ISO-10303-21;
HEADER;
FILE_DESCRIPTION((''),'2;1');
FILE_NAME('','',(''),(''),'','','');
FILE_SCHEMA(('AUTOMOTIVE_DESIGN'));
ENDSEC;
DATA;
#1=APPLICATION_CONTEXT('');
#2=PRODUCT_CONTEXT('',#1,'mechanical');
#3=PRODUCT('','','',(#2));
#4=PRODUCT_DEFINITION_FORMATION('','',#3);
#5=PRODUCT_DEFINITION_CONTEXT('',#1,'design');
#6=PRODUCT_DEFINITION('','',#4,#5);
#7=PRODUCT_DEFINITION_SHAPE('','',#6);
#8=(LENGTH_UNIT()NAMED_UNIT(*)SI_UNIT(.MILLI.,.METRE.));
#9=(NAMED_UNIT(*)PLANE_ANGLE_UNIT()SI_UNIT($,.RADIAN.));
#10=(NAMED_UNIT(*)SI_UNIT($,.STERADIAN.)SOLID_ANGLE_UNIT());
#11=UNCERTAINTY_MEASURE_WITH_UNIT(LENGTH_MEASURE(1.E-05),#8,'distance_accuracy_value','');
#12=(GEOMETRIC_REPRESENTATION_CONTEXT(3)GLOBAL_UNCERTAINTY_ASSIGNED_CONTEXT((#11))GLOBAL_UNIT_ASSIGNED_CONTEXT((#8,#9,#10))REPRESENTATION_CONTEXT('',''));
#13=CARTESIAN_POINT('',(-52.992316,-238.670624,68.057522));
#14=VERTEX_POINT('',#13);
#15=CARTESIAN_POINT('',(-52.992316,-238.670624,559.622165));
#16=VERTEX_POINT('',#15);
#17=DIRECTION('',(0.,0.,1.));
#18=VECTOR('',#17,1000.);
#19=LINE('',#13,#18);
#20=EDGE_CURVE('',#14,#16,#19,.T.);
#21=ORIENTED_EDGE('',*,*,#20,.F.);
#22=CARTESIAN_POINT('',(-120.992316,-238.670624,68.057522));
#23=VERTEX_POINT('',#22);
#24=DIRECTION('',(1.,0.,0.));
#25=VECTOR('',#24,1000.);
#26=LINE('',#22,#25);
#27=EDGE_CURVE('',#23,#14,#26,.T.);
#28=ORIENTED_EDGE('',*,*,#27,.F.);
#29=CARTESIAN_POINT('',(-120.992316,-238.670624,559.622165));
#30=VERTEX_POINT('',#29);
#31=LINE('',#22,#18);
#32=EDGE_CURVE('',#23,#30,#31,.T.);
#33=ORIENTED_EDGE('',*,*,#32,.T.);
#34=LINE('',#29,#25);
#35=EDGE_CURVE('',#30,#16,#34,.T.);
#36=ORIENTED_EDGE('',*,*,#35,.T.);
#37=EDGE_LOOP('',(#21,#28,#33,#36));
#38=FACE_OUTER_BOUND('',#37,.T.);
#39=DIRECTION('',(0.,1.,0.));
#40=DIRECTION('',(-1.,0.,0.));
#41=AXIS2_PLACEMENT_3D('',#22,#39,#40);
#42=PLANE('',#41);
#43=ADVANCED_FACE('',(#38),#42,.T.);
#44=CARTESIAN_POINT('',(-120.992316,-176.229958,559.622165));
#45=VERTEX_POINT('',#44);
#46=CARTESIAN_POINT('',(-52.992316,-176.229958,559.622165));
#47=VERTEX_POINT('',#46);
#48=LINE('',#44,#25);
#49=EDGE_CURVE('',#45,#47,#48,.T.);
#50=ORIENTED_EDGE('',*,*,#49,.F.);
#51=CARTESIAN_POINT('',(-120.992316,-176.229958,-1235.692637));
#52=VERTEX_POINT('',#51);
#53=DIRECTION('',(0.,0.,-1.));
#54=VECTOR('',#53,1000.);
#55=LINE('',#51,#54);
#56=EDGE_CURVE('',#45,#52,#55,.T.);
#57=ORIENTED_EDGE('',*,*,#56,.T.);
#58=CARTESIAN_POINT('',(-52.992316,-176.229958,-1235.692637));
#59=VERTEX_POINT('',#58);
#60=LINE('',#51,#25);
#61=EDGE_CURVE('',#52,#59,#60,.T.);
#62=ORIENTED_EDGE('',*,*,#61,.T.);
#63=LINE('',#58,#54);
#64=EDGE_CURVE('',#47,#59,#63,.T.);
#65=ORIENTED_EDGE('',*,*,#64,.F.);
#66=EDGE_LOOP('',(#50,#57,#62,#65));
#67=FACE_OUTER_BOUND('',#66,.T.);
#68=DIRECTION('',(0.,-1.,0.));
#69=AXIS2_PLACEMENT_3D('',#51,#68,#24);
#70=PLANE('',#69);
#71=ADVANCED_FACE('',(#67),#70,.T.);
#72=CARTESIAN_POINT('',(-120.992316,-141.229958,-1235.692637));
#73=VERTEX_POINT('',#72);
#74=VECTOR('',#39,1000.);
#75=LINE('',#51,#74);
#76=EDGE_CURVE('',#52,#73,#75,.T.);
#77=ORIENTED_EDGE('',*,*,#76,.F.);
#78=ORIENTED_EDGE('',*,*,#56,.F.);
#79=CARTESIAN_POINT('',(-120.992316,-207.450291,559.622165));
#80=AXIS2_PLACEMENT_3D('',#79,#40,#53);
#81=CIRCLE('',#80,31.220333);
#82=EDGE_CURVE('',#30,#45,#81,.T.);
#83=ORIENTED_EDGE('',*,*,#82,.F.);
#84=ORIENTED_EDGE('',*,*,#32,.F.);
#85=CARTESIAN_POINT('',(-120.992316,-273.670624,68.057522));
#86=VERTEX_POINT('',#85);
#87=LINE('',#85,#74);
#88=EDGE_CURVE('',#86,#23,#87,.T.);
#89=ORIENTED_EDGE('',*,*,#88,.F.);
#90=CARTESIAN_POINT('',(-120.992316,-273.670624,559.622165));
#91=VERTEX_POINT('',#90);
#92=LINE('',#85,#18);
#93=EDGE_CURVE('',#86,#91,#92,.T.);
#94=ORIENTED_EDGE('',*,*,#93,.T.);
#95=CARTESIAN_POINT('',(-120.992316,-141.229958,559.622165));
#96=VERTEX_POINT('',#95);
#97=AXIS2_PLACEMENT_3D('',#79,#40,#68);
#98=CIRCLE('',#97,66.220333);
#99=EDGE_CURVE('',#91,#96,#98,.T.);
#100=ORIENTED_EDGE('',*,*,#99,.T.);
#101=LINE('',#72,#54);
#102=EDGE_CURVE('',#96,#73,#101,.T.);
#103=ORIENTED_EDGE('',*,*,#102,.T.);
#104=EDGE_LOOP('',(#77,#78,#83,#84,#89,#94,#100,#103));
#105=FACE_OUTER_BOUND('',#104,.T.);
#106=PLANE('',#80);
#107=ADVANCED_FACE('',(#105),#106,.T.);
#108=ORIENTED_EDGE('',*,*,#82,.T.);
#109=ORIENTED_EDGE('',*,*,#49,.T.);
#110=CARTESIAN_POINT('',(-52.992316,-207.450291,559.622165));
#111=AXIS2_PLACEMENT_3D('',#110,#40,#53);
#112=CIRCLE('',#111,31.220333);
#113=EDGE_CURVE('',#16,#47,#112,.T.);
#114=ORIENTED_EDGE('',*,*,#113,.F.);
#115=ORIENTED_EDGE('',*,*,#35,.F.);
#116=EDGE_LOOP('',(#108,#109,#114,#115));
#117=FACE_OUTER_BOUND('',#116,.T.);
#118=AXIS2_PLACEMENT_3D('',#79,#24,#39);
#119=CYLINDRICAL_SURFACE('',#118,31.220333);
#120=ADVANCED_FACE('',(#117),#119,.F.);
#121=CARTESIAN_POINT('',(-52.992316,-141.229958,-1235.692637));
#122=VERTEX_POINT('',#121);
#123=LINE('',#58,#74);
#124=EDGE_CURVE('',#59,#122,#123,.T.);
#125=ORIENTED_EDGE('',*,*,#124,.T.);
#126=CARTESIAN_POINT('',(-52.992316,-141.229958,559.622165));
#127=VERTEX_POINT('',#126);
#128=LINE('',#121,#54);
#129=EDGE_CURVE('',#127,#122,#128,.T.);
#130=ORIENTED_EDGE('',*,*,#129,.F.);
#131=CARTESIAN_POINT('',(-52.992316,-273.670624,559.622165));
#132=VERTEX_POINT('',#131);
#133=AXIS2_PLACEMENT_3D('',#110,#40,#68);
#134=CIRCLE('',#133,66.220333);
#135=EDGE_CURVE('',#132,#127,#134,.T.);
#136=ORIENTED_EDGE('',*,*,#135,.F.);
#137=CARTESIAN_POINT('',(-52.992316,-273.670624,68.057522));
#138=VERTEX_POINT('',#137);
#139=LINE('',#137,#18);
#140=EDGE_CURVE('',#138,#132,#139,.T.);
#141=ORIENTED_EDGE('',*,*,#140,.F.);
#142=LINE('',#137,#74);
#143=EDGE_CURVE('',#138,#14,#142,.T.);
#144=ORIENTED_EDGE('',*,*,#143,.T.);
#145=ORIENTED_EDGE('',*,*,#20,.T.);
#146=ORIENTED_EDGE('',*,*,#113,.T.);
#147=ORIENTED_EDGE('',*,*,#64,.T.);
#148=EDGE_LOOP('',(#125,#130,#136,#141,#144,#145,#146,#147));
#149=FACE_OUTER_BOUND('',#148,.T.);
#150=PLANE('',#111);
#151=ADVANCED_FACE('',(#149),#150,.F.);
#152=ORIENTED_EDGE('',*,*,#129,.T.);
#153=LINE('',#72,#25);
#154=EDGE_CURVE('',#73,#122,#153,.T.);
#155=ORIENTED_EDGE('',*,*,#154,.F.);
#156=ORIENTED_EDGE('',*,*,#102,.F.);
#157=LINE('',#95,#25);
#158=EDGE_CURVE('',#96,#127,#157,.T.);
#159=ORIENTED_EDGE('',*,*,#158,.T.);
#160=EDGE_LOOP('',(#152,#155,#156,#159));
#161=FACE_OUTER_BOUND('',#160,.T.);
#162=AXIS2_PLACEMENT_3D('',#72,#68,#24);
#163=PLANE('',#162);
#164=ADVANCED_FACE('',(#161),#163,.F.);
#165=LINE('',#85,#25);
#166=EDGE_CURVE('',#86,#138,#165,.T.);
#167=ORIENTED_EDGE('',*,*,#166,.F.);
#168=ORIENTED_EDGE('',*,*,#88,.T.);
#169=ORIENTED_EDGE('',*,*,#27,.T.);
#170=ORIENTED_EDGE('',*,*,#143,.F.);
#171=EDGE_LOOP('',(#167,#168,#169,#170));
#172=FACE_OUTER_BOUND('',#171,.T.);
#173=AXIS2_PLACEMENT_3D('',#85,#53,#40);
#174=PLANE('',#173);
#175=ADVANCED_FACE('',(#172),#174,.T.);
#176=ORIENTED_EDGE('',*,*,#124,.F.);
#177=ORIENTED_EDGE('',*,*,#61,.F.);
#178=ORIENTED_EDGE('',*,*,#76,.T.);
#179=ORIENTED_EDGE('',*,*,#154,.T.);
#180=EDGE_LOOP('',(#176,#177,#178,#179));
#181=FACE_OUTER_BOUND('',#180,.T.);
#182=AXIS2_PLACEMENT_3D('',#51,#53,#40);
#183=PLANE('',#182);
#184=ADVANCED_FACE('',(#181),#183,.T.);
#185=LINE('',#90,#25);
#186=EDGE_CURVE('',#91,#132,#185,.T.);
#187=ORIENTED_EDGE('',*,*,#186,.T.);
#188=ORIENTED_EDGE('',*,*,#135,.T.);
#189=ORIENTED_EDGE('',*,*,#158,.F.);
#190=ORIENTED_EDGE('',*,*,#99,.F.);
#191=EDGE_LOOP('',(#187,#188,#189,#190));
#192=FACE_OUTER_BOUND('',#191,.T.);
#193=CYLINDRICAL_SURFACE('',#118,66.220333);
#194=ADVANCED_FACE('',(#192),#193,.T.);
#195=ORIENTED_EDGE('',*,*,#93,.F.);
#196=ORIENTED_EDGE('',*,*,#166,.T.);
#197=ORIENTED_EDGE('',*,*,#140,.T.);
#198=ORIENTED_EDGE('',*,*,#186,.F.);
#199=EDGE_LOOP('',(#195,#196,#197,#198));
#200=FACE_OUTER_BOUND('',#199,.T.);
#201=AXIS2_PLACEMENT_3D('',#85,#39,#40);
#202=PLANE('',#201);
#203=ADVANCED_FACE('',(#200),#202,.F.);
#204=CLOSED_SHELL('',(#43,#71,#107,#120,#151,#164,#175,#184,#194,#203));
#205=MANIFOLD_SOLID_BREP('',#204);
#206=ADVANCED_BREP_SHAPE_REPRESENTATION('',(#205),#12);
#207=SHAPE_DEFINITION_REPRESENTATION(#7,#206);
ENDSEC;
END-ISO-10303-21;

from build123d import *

# Parameters (mm, degrees)
EXTRUDE_1_DEPTH = 34


with BuildPart() as part:
    # 草图1 → 拉伸-薄壁1 (new, symmetric)
    with BuildSketch(Plane(origin=(-86.992315928, -141.229957863, -135.692636998), x_dir=(0, 0, -1), z_dir=(-1, 0, 0))):
        with BuildLine():
            Line((1100, 0), (-695.31480211, 0))
            ThreePointArc((-695.31480211, 0), (-761.535134985, 66.220332876), (-695.31480211, 132.440665751))
            Line((-695.31480211, 132.440665751), (-203.750159412, 132.440665751))
            Line((-203.750159412, 132.440665751), (-203.750159412, 97.440665751))
            Line((-203.750159412, 97.440665751), (-695.31480211, 97.440665751))
            ThreePointArc((-695.31480211, 97.440665751), (-726.535134985, 66.220332876), (-695.31480211, 35))
            Line((-695.31480211, 35), (1100, 35))
            Line((1100, 35), (1100, 0))
        make_face()
    extrude(amount=EXTRUDE_1_DEPTH, both=True)


solid = part.part
